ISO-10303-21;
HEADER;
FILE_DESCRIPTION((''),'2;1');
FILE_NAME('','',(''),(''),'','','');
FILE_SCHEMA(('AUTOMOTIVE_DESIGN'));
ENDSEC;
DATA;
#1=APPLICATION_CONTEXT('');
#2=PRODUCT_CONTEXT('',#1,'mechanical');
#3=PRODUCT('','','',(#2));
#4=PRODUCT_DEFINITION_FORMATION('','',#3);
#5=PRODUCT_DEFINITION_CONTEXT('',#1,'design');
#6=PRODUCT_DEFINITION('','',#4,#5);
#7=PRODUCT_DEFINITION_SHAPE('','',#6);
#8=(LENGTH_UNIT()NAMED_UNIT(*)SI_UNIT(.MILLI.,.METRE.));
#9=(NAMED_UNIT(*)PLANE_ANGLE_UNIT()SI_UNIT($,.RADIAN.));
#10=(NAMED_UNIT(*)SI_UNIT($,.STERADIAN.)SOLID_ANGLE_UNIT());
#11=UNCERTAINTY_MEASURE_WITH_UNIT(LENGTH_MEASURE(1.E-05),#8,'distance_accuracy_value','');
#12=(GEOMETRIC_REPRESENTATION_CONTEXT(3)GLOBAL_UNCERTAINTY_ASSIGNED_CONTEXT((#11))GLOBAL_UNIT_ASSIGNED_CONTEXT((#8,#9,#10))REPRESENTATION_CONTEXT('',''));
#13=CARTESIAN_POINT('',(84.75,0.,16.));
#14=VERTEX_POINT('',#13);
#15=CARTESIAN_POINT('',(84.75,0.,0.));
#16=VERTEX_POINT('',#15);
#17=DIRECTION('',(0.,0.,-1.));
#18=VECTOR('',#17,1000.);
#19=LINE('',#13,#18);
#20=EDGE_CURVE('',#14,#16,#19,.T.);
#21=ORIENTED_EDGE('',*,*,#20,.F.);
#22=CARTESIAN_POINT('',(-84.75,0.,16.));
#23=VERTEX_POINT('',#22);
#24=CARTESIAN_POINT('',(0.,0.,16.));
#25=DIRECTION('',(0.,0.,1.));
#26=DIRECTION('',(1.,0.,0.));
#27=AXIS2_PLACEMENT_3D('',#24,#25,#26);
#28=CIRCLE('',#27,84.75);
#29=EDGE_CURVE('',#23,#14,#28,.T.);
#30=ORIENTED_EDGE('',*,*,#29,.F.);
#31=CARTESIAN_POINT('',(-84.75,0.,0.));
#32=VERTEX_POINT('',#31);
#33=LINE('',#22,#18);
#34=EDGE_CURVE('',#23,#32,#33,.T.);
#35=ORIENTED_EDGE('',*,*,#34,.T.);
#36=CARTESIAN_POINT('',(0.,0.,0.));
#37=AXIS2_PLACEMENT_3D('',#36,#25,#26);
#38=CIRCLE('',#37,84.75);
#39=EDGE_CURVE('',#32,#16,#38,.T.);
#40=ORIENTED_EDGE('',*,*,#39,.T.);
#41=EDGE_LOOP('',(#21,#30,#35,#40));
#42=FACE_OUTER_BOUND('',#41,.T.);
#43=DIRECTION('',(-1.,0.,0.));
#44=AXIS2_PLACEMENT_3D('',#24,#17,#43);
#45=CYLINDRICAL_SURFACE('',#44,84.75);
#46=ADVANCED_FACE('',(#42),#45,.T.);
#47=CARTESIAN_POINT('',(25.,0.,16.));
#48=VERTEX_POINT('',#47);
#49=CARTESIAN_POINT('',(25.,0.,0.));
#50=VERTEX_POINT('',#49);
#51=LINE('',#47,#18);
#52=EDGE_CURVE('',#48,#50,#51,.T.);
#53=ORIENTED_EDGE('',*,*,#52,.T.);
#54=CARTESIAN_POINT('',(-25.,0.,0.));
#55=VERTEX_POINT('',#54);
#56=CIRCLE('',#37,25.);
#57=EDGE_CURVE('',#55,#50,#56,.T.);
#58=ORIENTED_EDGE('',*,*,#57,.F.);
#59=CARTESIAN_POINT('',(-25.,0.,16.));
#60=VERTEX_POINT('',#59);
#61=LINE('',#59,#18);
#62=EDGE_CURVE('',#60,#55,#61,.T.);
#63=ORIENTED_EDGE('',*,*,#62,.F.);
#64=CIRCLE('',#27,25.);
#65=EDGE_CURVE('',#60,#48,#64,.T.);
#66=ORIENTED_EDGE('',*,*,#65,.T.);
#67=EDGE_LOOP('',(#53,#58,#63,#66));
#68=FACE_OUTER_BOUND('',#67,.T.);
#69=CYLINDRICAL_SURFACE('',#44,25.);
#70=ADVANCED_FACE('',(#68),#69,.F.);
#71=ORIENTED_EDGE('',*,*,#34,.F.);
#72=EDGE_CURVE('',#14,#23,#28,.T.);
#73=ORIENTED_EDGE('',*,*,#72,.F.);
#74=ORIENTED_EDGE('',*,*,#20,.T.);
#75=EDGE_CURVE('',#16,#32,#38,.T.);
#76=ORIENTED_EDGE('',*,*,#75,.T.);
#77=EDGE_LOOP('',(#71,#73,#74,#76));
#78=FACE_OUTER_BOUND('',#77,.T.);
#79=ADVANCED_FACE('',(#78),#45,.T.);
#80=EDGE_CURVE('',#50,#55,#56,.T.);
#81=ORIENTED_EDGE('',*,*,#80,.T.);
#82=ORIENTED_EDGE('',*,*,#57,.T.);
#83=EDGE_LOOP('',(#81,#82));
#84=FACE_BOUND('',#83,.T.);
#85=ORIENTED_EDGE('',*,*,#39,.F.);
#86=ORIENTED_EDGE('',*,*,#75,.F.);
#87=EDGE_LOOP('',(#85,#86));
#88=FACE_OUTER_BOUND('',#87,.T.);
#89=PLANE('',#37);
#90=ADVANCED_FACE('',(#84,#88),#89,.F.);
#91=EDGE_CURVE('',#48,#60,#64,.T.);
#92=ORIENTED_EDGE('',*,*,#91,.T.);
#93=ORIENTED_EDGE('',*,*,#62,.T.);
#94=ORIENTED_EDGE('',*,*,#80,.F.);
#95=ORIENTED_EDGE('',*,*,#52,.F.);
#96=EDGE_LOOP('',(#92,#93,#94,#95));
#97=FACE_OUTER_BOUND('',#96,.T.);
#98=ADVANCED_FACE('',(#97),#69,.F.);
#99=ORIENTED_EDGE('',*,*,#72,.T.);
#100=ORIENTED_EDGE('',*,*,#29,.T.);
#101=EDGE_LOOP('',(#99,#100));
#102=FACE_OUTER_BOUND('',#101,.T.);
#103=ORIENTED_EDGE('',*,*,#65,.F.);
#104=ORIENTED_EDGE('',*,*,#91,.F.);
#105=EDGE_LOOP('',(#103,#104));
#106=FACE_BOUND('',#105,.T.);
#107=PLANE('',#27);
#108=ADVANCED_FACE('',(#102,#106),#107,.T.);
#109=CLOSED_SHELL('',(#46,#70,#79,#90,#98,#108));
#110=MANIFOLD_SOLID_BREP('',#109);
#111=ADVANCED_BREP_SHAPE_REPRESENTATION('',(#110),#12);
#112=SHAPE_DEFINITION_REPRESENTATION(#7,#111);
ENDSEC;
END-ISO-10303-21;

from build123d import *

# Parameters (mm, degrees)
SKETCH1_R           = 84.75
SKETCH1_R_2         = 25
BOSS_EXTRUDE1_DEPTH = 16


with BuildPart() as part:
    # Sketch1 → Boss-Extrude1 (new body)
    with BuildSketch(Plane.XY):
        Circle(SKETCH1_R)
        Circle(SKETCH1_R_2, mode=Mode.SUBTRACT)
    extrude(amount=BOSS_EXTRUDE1_DEPTH)


solid = part.part
